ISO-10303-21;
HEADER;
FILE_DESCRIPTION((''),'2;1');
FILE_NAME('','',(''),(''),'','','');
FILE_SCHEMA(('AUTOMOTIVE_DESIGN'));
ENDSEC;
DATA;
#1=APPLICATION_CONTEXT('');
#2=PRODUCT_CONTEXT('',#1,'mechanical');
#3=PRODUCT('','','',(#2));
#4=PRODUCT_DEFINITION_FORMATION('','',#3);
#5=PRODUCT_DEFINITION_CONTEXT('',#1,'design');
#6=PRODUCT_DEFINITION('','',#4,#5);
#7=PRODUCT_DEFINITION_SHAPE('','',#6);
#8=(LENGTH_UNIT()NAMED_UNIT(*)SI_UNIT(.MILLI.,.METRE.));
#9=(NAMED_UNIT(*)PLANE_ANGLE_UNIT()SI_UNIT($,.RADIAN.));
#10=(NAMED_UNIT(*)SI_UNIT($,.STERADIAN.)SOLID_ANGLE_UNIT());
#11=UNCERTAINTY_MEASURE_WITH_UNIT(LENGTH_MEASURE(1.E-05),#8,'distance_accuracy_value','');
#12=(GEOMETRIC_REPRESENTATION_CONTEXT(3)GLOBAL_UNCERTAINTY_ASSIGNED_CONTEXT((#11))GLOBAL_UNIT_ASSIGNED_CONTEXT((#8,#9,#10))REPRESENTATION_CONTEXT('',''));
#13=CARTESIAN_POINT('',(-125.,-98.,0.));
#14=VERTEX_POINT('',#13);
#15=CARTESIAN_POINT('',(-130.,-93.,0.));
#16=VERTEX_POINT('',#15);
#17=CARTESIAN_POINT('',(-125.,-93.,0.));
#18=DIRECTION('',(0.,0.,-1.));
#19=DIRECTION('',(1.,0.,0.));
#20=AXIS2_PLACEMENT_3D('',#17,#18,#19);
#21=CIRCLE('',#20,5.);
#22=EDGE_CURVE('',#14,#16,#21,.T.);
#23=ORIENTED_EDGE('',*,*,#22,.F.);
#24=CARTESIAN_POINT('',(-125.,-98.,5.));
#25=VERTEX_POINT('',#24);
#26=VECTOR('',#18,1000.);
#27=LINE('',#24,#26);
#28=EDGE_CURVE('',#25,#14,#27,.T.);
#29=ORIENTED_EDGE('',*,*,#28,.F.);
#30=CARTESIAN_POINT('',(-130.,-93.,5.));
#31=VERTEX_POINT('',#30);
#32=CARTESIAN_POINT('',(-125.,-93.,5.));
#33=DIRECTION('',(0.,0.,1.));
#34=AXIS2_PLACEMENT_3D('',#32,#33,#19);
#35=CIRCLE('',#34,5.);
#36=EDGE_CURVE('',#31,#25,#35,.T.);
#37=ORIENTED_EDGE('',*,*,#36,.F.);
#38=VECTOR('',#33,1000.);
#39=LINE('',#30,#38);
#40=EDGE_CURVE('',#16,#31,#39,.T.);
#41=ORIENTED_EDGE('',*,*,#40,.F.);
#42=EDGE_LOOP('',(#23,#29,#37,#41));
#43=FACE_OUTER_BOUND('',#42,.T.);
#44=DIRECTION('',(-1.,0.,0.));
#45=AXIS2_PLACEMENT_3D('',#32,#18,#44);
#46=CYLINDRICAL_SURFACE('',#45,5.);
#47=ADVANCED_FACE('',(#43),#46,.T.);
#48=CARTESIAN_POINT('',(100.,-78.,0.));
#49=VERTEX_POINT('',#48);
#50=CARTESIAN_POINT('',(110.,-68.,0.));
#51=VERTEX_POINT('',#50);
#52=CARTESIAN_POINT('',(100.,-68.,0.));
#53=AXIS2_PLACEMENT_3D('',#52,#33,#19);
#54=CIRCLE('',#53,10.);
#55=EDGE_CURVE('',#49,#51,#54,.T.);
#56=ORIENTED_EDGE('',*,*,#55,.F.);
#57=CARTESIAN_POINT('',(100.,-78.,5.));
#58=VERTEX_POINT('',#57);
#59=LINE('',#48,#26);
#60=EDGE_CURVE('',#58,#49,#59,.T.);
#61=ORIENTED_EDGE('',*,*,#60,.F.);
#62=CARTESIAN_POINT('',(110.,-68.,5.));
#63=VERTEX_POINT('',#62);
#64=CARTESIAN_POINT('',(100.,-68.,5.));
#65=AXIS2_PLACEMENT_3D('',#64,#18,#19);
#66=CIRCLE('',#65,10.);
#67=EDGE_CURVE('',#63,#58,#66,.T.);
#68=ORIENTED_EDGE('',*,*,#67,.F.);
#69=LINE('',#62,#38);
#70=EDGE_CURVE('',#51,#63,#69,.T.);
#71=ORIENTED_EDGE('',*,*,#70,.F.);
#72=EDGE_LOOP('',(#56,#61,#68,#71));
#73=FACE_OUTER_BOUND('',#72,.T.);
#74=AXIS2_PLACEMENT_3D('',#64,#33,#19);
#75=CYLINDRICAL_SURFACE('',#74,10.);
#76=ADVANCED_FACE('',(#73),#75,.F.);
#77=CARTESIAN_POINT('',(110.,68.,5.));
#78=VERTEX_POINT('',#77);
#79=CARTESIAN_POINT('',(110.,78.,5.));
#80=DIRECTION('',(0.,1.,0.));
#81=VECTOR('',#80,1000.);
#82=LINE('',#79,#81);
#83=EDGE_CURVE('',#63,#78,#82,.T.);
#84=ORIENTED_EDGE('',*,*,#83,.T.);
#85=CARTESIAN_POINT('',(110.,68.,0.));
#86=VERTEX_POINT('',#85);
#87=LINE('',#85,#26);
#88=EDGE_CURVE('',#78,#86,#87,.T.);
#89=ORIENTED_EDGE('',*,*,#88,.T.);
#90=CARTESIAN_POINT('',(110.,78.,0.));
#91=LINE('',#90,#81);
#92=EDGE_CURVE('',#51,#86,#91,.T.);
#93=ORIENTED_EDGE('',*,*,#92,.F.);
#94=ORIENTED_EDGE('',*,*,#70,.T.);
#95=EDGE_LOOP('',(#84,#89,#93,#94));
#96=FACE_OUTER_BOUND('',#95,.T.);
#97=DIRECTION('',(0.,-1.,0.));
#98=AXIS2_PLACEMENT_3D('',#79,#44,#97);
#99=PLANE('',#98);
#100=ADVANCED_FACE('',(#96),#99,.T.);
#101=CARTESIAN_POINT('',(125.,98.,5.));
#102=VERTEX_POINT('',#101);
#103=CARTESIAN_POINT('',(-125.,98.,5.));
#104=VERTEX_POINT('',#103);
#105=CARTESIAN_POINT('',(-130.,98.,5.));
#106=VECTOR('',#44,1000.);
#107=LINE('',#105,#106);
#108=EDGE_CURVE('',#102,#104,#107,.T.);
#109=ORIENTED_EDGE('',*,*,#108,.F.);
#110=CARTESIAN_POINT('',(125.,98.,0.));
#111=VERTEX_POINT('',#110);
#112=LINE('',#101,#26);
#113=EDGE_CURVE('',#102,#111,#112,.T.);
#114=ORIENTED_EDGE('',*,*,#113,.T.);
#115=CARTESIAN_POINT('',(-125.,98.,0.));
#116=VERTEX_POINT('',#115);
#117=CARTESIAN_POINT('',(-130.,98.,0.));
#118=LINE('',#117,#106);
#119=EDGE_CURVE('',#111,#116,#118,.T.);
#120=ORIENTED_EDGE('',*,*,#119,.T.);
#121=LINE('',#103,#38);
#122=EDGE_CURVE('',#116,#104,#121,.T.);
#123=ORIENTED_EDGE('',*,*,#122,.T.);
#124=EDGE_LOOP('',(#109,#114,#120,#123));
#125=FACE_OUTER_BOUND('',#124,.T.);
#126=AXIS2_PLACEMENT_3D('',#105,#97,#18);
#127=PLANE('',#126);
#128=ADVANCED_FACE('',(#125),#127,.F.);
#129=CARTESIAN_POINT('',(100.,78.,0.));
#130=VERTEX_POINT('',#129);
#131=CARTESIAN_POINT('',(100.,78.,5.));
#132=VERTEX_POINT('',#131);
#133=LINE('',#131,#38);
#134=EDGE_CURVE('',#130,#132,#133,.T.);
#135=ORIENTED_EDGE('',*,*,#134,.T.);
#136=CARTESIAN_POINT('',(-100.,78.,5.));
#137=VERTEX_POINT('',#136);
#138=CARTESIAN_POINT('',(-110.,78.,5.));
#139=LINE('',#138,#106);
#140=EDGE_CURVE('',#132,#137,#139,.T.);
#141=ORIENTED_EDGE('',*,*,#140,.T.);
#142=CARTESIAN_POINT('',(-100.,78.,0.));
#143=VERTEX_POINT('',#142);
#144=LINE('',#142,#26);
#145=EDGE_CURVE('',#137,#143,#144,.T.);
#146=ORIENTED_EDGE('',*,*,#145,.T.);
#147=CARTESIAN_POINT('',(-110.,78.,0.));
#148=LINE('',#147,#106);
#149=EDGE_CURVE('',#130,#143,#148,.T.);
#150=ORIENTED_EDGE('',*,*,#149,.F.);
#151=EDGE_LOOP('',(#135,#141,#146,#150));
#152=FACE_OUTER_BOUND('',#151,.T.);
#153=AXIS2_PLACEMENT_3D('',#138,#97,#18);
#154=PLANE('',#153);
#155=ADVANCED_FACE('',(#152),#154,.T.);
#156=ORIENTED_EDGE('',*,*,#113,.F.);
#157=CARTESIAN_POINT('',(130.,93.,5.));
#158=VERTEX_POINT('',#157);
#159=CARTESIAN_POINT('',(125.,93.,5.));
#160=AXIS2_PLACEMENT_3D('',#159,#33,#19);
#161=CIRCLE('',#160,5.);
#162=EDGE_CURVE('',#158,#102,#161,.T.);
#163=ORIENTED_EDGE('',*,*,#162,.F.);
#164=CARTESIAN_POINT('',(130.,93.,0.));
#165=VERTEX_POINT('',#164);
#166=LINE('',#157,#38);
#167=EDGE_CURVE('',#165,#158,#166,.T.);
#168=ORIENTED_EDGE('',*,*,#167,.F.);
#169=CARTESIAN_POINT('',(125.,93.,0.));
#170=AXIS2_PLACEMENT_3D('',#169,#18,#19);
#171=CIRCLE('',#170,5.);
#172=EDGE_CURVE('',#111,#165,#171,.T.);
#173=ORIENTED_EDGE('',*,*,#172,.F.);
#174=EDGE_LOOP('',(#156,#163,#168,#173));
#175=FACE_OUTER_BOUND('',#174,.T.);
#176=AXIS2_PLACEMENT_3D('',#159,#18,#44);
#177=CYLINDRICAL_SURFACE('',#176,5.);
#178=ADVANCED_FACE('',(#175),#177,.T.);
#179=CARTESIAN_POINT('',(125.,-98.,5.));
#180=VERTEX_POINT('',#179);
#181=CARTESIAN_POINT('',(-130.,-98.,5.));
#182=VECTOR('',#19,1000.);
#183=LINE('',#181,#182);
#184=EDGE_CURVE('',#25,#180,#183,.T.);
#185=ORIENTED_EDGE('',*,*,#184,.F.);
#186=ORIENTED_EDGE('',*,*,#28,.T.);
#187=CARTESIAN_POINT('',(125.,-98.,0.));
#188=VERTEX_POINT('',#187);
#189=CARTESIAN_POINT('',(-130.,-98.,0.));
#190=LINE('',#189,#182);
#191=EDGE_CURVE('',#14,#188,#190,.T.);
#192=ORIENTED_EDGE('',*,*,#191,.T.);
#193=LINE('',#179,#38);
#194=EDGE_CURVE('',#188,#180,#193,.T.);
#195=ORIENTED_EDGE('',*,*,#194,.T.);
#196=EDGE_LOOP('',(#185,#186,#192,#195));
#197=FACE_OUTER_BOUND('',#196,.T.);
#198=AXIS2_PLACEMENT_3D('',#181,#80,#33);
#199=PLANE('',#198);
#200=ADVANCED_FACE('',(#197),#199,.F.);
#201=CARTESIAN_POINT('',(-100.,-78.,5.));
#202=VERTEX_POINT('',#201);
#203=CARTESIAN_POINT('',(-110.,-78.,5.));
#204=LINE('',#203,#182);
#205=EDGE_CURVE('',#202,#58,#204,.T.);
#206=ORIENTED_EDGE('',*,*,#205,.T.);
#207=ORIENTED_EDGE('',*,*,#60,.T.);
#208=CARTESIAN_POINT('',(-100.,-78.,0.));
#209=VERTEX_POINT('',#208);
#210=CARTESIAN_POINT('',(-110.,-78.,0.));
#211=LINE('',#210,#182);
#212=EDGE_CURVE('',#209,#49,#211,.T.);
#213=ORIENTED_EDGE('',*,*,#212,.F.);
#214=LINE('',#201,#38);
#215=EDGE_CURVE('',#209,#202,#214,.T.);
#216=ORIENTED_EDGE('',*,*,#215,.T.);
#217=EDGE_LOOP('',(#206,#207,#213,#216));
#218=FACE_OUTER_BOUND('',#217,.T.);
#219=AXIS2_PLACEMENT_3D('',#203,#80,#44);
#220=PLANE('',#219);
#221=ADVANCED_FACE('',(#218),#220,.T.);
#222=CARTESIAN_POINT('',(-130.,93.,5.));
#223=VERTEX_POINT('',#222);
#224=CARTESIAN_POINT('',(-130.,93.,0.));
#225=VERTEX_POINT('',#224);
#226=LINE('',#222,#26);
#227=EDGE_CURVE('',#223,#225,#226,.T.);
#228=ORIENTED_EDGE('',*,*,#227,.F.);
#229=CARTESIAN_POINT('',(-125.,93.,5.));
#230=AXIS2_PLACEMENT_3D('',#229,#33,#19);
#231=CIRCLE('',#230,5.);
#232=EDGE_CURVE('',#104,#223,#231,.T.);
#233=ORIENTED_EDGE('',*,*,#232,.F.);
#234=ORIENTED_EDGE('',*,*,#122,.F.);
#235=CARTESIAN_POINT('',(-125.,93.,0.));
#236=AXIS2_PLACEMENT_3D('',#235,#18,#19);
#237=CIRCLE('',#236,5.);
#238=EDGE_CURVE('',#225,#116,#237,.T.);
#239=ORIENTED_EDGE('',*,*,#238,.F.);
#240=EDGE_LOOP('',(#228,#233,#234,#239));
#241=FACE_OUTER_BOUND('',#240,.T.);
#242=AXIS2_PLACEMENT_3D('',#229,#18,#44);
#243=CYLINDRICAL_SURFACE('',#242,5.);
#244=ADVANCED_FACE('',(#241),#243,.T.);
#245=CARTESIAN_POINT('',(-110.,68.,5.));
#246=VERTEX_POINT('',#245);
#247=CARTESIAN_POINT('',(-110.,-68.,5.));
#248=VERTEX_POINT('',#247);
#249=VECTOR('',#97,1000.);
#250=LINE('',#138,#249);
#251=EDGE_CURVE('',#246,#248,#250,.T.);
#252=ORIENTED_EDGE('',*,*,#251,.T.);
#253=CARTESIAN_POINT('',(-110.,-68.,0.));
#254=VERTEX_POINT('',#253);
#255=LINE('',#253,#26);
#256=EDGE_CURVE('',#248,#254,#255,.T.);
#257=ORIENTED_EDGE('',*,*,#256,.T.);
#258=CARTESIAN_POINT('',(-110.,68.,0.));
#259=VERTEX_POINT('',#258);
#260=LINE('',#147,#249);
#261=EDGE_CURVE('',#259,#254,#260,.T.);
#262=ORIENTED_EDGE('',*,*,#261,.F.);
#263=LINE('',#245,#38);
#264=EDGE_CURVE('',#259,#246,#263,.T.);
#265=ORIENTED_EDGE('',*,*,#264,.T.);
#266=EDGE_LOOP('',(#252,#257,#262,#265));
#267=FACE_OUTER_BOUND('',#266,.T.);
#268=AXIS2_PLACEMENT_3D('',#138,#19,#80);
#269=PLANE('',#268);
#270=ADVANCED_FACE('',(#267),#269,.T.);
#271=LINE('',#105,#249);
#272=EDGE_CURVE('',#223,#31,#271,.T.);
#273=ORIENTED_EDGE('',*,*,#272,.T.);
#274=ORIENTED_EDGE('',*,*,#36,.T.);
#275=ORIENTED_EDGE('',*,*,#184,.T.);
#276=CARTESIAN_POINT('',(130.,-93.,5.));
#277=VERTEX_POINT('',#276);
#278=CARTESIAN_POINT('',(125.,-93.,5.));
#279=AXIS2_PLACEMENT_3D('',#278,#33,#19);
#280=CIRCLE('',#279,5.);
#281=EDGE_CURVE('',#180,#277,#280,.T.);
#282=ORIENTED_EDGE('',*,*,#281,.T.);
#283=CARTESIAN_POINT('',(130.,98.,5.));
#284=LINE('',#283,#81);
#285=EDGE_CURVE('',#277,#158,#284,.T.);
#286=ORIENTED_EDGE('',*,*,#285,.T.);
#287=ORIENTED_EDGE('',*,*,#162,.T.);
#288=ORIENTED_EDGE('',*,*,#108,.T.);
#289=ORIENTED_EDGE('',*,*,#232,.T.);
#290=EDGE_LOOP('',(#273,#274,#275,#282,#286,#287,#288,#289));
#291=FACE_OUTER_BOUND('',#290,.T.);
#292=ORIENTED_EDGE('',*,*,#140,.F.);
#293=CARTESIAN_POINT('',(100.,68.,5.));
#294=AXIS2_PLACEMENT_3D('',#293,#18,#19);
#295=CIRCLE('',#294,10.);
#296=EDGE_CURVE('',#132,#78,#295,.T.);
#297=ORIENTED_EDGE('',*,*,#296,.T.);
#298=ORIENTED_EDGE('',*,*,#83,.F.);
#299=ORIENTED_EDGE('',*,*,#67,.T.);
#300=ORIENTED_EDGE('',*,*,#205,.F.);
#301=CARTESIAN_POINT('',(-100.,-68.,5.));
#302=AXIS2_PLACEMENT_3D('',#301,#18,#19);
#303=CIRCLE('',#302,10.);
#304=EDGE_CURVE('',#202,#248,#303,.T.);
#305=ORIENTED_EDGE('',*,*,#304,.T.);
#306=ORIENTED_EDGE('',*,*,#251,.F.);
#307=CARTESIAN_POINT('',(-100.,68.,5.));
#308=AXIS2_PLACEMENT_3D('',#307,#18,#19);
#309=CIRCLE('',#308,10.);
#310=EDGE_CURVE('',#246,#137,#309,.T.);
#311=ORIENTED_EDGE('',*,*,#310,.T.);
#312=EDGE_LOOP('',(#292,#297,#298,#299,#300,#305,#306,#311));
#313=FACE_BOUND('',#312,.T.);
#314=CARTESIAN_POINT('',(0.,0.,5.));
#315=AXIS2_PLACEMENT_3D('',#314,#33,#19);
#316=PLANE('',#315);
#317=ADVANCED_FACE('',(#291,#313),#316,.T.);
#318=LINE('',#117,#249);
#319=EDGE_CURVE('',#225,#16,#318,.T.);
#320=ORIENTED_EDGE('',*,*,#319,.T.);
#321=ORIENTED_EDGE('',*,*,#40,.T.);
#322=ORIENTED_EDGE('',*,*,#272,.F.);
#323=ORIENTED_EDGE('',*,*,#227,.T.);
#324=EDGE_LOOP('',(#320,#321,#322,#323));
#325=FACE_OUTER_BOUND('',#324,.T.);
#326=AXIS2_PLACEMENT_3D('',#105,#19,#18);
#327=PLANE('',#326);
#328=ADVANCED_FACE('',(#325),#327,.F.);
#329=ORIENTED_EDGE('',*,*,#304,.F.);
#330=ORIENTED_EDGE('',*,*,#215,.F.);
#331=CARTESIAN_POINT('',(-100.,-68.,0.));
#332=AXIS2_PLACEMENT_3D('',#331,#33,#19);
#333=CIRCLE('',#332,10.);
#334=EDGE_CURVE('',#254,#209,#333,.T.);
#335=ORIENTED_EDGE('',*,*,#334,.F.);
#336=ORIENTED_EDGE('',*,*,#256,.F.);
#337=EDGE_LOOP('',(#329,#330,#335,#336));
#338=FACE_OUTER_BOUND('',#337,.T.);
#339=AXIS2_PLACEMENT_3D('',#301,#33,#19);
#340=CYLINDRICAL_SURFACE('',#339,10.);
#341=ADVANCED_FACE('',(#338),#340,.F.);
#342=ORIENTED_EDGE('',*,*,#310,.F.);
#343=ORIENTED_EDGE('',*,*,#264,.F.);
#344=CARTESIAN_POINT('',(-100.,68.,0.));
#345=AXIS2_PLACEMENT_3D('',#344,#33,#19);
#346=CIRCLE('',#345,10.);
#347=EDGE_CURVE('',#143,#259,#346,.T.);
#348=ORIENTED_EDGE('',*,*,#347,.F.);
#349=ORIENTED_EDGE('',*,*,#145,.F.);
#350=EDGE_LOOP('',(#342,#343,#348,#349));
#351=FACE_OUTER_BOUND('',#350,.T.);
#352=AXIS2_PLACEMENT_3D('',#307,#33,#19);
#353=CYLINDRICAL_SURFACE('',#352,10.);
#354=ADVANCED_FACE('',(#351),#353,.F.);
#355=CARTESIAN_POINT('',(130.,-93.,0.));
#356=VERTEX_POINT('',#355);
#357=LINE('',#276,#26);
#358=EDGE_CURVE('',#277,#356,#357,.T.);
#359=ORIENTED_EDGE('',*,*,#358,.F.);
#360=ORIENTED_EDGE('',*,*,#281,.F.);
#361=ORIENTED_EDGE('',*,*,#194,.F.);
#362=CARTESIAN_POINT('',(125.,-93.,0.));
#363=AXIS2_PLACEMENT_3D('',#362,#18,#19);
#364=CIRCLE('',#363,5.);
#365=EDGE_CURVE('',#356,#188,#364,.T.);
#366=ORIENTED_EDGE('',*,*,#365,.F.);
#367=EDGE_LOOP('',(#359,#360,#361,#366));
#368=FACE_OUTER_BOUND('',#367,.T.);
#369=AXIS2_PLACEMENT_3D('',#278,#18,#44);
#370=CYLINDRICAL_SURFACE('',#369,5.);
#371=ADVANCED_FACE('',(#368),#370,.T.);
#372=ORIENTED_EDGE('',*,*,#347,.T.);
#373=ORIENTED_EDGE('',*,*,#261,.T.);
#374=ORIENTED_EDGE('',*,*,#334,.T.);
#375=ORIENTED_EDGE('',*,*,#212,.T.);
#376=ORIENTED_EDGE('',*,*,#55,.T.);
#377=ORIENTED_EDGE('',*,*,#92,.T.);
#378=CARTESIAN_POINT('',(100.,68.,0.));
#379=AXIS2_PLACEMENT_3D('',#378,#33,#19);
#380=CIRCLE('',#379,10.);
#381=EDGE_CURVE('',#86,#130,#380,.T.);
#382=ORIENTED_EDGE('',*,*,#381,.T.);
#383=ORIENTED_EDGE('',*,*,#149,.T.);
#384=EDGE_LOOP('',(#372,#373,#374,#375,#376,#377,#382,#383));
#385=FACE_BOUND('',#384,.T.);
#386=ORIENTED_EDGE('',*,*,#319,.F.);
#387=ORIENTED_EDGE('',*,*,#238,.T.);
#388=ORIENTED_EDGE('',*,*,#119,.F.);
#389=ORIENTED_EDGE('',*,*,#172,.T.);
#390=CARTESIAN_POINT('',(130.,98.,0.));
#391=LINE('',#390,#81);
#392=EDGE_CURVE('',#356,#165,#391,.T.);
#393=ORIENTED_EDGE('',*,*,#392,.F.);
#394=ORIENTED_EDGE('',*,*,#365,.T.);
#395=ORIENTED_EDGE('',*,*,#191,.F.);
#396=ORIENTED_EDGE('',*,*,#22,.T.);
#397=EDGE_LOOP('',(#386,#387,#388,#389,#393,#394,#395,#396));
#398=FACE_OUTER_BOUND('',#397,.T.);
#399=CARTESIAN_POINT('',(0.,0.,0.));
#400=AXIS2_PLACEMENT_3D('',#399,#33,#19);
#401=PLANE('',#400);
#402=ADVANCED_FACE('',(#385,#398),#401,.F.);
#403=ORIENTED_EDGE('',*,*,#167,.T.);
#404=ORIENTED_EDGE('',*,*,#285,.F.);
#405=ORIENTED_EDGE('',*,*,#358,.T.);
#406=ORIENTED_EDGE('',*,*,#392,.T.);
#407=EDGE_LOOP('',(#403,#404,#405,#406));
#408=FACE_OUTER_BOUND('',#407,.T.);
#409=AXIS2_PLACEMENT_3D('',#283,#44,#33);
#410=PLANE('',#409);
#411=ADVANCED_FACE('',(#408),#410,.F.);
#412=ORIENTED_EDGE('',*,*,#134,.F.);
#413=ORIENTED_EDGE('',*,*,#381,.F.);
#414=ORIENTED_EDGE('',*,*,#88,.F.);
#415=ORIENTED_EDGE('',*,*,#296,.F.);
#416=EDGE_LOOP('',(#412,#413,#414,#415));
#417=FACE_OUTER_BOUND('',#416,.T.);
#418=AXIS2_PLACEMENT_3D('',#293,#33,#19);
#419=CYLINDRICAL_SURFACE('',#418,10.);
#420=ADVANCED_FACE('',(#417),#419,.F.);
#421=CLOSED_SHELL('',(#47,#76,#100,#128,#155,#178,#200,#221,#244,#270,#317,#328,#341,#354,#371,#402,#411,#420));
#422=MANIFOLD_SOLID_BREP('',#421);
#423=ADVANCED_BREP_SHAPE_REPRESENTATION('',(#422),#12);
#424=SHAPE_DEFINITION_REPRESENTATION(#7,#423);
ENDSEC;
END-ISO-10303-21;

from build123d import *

# Parameters (mm, degrees)
SKETCH1_W           = 260
SKETCH1_H           = 196
SKETCH1_W_2         = 220
SKETCH1_H_2         = 156
BOSS_EXTRUDE1_DEPTH = 5
FILLET1_R           = 5
FILLET2_R           = 10


with BuildPart() as part:
    # Sketch1 → Boss-Extrude1 (new body)
    with BuildSketch(Plane.XY):
        Rectangle(SKETCH1_W, SKETCH1_H)
        Rectangle(SKETCH1_W_2, SKETCH1_H_2, mode=Mode.SUBTRACT)
    extrude(amount=BOSS_EXTRUDE1_DEPTH)

    # Fillet1
    fillet1_edges = [part.edges().sort_by_distance(p)[0] for p in [
        (-130, 98, 2.5),
        (130, 98, 2.5),
        (130, -98, 2.5),
        (-130, -98, 2.5),
    ]]
    fillet(fillet1_edges, radius=FILLET1_R)

    # Fillet2
    fillet2_edges = [part.edges().sort_by_distance(p)[0] for p in [
        (-110, 78, 2.5),
        (-110, -78, 2.5),
        (110, -78, 2.5),
        (110, 78, 2.5),
    ]]
    fillet(fillet2_edges, radius=FILLET2_R)


solid = part.part
